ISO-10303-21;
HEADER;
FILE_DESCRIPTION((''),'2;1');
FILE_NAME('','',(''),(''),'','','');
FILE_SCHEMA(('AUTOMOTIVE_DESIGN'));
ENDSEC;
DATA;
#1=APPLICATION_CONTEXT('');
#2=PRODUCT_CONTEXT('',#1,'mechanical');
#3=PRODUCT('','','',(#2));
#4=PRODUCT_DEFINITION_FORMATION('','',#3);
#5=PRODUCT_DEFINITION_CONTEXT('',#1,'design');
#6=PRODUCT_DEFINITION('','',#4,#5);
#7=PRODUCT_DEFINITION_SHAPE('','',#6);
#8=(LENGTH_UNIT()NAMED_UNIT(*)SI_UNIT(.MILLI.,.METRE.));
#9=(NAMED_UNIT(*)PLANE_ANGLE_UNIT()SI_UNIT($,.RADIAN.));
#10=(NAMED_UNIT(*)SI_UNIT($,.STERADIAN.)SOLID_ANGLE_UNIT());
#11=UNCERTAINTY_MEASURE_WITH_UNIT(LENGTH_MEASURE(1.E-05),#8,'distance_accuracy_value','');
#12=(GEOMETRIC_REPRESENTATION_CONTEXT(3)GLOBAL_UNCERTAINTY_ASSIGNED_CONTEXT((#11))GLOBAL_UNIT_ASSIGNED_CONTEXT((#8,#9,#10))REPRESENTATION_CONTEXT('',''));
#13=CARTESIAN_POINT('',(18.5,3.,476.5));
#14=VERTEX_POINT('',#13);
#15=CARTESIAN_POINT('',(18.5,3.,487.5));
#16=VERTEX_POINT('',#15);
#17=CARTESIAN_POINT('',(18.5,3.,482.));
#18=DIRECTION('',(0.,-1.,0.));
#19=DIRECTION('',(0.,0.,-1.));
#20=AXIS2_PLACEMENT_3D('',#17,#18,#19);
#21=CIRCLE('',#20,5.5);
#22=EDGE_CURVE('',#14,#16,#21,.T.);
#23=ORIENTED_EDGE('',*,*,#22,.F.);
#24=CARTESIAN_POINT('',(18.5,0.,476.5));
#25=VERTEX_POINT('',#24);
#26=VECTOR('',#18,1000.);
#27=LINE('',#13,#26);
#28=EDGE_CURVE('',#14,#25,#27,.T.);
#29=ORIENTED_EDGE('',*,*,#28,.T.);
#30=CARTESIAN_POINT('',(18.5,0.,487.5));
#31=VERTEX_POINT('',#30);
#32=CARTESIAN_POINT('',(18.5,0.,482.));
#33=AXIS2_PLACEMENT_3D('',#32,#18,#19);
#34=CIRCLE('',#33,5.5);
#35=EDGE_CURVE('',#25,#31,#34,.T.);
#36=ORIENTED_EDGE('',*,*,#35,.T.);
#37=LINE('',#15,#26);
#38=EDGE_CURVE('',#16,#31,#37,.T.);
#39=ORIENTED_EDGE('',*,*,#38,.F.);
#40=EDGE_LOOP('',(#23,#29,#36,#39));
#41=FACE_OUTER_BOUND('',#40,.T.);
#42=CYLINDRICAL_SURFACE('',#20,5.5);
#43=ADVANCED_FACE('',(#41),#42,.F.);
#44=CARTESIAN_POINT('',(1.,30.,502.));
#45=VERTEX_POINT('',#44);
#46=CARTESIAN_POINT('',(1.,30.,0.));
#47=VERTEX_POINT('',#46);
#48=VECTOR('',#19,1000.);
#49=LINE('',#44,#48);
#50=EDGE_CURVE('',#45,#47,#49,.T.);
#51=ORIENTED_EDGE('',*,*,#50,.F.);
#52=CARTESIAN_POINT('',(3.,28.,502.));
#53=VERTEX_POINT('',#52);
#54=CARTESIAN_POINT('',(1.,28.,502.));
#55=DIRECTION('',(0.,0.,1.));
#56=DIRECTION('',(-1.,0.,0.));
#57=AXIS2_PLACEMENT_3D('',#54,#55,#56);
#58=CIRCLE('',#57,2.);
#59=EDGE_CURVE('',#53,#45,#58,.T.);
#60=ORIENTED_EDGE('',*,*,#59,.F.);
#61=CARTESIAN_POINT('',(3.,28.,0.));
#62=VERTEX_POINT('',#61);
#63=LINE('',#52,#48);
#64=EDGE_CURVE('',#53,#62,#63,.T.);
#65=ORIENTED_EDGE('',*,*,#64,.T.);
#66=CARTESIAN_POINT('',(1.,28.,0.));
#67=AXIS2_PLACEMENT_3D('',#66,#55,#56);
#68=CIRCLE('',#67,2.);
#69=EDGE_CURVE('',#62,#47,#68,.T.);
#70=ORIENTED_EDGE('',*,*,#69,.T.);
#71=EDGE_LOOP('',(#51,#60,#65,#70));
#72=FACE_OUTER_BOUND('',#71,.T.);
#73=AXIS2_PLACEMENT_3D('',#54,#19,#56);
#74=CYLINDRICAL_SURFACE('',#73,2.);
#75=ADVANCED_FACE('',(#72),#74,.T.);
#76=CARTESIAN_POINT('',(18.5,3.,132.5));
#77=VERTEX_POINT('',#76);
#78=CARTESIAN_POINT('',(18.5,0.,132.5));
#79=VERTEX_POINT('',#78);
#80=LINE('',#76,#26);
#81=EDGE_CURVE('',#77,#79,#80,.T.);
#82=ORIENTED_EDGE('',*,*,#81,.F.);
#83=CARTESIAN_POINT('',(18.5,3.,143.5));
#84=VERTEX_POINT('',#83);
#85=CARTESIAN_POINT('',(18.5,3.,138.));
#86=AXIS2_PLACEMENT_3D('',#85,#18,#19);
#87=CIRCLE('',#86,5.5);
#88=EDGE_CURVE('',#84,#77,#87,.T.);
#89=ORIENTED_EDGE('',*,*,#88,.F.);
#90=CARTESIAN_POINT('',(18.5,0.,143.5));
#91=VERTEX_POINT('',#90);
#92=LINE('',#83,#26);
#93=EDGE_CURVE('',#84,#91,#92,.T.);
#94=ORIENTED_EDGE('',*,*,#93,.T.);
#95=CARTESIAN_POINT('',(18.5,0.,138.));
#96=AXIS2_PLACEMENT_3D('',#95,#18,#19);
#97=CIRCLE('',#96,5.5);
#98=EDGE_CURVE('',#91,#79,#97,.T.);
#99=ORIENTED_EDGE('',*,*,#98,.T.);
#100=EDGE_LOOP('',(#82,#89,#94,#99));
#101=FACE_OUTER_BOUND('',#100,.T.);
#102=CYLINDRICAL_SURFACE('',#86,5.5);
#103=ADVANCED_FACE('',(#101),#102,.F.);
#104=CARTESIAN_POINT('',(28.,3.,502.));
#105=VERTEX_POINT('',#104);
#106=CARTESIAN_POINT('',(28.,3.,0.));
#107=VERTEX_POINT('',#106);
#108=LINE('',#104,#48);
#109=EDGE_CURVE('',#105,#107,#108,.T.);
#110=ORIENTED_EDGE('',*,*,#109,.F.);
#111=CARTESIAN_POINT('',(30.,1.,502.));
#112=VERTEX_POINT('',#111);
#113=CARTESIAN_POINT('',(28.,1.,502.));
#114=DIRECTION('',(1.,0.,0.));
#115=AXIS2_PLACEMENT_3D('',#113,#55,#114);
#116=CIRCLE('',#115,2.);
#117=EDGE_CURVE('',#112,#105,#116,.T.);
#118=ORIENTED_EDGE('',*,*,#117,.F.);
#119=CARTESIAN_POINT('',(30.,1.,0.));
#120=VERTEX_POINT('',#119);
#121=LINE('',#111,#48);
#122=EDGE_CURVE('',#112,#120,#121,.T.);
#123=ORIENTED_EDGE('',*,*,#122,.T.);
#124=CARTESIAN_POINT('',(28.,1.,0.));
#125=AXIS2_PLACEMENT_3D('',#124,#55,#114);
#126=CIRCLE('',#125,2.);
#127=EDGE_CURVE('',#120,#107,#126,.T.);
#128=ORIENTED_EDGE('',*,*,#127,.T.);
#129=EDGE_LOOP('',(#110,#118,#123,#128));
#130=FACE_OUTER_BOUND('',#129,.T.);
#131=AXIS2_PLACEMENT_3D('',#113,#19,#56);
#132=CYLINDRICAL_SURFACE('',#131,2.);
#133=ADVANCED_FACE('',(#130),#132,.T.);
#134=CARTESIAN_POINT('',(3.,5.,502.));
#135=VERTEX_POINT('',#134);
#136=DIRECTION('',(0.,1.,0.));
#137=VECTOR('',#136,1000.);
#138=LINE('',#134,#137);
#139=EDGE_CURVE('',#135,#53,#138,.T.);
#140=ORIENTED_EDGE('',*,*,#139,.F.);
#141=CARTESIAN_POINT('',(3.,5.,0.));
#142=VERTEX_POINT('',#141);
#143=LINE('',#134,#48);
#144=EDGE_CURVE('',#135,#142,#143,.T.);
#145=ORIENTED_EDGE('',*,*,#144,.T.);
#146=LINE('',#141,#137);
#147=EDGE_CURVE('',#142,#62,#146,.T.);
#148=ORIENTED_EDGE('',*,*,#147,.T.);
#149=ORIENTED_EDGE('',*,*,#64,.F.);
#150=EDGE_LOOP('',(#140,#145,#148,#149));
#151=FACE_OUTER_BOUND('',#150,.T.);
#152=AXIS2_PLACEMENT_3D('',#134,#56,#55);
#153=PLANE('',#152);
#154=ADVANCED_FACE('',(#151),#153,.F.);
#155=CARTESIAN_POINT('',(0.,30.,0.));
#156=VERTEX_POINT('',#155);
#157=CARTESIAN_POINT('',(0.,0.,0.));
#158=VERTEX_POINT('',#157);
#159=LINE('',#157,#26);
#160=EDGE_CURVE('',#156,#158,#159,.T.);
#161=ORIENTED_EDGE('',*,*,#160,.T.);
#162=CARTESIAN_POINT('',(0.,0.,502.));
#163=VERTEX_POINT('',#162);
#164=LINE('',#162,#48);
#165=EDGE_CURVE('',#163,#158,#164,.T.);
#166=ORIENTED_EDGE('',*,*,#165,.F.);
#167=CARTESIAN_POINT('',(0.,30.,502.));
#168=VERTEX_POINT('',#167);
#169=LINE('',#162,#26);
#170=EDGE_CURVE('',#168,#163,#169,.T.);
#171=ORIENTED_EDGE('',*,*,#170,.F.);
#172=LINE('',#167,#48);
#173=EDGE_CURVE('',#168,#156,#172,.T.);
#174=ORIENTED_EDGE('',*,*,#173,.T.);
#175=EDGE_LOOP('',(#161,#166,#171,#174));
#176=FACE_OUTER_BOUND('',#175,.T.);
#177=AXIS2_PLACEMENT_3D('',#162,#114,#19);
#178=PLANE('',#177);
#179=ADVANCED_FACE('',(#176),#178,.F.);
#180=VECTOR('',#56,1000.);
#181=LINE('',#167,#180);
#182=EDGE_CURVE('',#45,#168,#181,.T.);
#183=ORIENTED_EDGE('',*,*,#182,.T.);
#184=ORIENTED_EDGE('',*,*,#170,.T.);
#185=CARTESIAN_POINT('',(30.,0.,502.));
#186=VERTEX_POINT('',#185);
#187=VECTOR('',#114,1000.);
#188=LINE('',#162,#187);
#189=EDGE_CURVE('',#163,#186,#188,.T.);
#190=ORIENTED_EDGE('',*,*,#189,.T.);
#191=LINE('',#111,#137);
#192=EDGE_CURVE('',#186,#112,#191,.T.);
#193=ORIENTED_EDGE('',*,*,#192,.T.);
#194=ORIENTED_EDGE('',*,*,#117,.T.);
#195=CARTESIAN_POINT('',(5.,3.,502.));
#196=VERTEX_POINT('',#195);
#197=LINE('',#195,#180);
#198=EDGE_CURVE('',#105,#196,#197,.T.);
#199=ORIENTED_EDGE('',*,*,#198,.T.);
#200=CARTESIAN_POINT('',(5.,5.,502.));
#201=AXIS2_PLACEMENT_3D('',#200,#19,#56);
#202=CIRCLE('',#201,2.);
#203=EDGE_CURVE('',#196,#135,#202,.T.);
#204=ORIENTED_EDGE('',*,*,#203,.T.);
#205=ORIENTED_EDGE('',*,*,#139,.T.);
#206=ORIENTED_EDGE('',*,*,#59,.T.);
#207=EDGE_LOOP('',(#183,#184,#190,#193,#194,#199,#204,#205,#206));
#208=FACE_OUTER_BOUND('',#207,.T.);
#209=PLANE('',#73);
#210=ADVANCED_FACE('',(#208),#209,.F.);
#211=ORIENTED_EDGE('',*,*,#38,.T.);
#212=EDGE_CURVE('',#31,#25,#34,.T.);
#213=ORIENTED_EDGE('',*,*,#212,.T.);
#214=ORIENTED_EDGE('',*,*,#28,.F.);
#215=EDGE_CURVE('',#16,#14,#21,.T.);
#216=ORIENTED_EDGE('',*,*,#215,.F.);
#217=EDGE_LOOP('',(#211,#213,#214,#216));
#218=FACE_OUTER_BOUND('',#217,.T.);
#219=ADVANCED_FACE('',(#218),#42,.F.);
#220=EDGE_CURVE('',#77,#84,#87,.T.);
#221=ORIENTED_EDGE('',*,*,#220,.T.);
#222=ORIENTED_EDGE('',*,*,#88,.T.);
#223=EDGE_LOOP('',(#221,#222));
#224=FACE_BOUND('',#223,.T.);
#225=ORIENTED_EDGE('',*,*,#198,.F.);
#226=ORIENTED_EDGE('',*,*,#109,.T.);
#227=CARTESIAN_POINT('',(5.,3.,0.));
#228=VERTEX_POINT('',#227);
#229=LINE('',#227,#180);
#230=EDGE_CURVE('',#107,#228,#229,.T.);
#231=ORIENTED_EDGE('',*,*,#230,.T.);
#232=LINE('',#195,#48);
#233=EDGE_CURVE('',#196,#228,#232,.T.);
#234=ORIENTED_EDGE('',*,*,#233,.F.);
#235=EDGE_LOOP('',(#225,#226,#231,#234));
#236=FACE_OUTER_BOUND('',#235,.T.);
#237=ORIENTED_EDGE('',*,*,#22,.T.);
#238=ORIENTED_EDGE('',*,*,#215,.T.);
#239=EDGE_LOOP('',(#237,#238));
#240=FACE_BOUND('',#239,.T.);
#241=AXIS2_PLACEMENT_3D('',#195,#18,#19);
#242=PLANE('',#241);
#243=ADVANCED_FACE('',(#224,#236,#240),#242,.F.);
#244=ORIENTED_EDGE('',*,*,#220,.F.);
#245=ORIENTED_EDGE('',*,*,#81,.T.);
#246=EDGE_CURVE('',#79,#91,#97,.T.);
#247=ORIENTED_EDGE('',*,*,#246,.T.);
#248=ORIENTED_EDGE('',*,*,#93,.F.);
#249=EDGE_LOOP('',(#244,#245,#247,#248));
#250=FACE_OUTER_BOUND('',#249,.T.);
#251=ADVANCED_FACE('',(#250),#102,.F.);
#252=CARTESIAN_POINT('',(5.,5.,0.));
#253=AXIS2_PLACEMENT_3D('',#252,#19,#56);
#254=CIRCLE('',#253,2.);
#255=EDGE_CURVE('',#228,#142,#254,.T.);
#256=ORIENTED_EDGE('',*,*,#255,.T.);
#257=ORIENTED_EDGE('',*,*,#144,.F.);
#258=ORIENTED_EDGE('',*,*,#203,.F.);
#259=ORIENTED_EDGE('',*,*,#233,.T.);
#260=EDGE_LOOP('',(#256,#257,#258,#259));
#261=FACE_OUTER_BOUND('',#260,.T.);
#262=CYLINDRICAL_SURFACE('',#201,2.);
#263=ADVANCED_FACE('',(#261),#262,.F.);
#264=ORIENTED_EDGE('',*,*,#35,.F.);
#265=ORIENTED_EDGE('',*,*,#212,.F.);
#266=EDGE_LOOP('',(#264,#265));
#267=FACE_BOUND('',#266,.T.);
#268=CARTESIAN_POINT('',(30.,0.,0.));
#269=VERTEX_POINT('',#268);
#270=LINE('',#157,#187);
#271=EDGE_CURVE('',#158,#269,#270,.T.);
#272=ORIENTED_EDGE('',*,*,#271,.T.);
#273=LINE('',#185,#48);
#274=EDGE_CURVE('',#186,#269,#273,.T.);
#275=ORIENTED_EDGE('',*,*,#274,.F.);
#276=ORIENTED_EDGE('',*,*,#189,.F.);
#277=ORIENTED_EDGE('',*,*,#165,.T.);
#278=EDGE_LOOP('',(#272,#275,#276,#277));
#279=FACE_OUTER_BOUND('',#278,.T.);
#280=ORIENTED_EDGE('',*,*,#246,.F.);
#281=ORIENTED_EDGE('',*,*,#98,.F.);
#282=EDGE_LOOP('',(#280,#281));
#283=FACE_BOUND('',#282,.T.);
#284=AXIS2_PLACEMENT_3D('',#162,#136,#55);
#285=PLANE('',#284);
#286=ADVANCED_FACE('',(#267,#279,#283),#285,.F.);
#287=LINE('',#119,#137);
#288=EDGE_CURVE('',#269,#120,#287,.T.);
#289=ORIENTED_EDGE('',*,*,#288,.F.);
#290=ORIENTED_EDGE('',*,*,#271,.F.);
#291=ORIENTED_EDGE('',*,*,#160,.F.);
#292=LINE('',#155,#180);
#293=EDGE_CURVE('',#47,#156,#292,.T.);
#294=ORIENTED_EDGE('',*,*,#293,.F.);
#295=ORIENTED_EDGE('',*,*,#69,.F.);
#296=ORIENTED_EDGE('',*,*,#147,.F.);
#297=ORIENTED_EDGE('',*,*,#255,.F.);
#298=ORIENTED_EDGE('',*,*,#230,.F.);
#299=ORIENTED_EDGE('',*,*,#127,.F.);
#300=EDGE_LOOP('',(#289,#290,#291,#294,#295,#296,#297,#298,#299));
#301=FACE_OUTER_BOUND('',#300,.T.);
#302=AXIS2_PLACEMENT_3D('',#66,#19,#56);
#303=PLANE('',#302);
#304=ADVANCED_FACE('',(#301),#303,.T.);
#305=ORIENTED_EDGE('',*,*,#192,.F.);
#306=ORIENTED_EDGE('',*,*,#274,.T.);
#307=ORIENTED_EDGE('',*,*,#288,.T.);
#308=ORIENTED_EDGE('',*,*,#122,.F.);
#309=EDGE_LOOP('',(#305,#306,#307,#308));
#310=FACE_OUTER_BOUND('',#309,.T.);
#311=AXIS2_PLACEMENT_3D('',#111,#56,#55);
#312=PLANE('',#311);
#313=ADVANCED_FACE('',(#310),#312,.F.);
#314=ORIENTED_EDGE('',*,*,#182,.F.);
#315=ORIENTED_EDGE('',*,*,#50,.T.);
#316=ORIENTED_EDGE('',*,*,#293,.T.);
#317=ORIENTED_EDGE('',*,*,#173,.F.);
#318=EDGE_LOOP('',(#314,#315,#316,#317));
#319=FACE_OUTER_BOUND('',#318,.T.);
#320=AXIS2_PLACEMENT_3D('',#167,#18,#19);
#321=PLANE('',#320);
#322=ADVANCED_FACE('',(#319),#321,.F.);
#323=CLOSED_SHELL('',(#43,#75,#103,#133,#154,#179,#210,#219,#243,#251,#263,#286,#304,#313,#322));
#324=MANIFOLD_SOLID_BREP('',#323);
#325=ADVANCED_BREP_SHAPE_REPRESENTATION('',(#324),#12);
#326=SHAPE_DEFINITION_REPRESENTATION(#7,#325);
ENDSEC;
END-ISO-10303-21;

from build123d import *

# Parameters (mm, degrees)
BOSS_EXTRUDE1_DEPTH = 502
SKETCH2_R           = 5.5
CUT_EXTRUDE1_DEPTH  = 3
LPATTERN1_COUNT     = 2
LPATTERN1_PITCH     = 344


with BuildPart() as part:
    # Sketch1 → Boss-Extrude1 (new body)
    with BuildSketch(Plane.XY):
        with BuildLine():
            Line((0, 0), (30, 0))
            Line((30, 0), (30, 1))
            ThreePointArc((30, 1), (29.414213562, 2.414213562), (28, 3))
            Line((28, 3), (5, 3))
            ThreePointArc((5, 3), (3.585786438, 3.585786438), (3, 5))
            Line((3, 5), (3, 28))
            ThreePointArc((3, 28), (2.414213562, 29.414213562), (1, 30))
            Line((1, 30), (0, 30))
            Line((0, 30), (0, 0))
        make_face()
    extrude(amount=BOSS_EXTRUDE1_DEPTH)

    # Sketch2 → Cut-Extrude1 (cut)
    with BuildSketch(Plane.XZ):
        with Locations(Location((18.5, 482, 0), (0, 0, 270))):
            Circle(SKETCH2_R)
    cut_extrude1 = extrude(amount=-CUT_EXTRUDE1_DEPTH, mode=Mode.SUBTRACT)

    # LPattern1: Cut-Extrude1 ×2
    with Locations(*[(0, 0, -i * LPATTERN1_PITCH) for i in range(1, LPATTERN1_COUNT)]):
        add(cut_extrude1, mode=Mode.SUBTRACT)


solid = part.part
